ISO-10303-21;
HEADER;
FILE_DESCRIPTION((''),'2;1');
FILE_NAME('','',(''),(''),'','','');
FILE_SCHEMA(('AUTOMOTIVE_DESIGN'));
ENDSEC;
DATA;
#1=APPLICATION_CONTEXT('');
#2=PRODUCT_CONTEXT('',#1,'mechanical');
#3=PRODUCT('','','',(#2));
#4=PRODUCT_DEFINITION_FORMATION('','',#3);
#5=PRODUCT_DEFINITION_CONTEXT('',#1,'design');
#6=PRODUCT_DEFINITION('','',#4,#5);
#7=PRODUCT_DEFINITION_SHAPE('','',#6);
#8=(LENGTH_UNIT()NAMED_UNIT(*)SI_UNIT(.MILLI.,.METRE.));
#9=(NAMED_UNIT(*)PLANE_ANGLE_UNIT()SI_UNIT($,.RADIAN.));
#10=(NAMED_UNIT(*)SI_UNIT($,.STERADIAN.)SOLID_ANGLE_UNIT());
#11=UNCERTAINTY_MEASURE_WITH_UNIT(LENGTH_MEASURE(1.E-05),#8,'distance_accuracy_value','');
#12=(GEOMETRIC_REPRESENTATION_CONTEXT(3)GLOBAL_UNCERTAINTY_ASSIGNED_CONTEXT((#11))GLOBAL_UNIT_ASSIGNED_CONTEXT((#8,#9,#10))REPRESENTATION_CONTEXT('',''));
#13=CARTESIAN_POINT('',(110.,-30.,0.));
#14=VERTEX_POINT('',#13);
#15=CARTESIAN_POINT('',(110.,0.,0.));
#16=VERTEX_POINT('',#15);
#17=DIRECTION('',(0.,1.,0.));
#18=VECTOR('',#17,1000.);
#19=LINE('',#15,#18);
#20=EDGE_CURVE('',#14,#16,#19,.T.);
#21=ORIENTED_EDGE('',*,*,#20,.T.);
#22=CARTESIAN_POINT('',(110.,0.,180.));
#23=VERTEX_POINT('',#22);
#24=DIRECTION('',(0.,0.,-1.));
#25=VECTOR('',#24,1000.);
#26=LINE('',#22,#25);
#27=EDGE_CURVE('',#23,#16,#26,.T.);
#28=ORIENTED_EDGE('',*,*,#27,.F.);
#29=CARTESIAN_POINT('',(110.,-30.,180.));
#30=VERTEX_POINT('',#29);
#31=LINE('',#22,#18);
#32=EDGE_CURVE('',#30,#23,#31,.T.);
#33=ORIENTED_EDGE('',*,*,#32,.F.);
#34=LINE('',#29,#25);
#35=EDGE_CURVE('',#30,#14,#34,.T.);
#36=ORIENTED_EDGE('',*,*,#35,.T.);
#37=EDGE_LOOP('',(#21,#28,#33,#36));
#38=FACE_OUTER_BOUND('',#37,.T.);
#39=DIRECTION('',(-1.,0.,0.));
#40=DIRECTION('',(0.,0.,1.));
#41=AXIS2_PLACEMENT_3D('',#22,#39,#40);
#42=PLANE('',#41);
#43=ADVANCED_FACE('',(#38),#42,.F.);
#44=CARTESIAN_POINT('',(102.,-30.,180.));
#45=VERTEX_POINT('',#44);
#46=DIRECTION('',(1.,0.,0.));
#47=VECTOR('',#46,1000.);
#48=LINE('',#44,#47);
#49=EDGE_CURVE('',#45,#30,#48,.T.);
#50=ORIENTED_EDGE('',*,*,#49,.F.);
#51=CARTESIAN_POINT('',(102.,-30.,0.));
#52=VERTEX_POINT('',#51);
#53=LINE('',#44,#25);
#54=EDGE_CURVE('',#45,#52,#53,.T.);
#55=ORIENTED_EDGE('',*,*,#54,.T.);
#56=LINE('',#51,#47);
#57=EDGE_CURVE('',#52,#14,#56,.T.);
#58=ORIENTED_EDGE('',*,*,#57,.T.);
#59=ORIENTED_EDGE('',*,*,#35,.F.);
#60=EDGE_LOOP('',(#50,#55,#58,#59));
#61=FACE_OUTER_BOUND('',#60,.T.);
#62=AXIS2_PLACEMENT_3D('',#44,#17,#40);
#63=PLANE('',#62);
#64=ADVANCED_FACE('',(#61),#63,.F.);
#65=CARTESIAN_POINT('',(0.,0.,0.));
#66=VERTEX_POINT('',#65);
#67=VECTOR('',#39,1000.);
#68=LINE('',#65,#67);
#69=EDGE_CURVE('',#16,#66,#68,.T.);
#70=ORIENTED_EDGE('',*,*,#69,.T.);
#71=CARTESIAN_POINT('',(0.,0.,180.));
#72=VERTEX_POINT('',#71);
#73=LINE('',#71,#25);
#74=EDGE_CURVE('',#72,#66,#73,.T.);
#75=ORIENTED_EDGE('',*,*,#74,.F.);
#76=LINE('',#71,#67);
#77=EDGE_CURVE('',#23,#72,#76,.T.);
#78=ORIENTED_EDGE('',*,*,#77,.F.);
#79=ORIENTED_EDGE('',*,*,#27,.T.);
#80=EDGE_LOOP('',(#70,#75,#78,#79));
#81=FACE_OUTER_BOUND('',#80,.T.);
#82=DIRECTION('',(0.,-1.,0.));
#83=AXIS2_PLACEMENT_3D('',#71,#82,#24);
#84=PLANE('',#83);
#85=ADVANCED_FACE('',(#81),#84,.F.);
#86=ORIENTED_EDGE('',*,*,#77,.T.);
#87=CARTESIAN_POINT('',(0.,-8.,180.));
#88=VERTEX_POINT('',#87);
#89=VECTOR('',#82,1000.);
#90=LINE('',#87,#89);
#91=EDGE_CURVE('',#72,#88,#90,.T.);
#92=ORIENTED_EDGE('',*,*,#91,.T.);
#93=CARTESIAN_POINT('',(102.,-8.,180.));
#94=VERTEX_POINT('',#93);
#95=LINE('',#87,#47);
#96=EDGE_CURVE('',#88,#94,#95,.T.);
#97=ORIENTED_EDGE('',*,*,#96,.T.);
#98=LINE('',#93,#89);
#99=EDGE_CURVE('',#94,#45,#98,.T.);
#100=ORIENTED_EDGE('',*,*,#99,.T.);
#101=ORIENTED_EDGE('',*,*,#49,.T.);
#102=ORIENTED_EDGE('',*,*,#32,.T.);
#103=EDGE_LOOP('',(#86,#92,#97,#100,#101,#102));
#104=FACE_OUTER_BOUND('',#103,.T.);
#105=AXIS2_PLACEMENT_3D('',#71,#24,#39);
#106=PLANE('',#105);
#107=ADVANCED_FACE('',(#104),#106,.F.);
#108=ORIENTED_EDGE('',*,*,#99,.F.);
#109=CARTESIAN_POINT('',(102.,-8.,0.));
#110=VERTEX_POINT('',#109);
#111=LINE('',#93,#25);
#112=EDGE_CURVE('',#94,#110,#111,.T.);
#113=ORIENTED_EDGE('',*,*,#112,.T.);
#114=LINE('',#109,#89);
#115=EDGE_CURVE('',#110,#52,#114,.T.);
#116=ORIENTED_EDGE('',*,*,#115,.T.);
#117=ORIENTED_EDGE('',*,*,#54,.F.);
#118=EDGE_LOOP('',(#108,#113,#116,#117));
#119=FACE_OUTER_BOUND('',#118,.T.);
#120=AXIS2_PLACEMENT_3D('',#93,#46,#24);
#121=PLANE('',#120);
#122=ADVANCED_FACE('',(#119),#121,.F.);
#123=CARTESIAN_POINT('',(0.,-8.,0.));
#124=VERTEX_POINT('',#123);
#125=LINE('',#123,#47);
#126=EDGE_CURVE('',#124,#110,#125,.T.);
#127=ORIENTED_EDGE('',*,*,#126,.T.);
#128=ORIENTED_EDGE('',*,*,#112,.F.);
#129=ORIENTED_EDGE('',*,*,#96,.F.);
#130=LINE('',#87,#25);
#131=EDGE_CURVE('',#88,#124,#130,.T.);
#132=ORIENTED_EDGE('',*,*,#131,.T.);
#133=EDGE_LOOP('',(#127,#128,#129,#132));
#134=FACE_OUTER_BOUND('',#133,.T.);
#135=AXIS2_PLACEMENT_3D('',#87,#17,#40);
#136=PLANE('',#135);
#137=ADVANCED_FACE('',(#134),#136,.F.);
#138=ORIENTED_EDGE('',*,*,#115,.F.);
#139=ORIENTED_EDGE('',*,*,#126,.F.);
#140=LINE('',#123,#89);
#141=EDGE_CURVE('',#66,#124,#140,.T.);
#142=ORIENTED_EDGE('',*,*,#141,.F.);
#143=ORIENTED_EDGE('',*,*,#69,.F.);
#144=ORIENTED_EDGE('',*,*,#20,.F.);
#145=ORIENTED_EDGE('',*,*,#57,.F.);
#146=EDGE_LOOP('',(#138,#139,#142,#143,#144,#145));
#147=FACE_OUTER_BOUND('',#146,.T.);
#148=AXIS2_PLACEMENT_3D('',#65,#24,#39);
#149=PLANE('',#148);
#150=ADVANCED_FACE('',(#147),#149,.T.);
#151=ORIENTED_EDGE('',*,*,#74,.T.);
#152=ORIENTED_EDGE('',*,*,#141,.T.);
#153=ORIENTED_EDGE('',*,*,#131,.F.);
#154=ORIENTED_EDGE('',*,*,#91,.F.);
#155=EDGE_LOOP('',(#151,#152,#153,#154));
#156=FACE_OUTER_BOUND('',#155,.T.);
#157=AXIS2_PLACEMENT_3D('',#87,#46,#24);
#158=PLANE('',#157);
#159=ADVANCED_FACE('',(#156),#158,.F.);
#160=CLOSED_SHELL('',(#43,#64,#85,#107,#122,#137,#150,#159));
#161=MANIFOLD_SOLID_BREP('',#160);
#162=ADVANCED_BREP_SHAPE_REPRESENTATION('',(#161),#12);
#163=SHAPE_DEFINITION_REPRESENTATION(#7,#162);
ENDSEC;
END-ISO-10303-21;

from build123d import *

# Parameters (mm, degrees)
EXTRUDE_1_DEPTH = 180


with BuildPart() as part:
    # 草图1 → 凸台-拉伸1 (new body)
    with BuildSketch(Plane.XY):
        Polygon((0, 0), (110, 0), (110, -30), (102, -30), (102, -8), (0, -8), align=None)
    extrude(amount=EXTRUDE_1_DEPTH)


solid = part.part
